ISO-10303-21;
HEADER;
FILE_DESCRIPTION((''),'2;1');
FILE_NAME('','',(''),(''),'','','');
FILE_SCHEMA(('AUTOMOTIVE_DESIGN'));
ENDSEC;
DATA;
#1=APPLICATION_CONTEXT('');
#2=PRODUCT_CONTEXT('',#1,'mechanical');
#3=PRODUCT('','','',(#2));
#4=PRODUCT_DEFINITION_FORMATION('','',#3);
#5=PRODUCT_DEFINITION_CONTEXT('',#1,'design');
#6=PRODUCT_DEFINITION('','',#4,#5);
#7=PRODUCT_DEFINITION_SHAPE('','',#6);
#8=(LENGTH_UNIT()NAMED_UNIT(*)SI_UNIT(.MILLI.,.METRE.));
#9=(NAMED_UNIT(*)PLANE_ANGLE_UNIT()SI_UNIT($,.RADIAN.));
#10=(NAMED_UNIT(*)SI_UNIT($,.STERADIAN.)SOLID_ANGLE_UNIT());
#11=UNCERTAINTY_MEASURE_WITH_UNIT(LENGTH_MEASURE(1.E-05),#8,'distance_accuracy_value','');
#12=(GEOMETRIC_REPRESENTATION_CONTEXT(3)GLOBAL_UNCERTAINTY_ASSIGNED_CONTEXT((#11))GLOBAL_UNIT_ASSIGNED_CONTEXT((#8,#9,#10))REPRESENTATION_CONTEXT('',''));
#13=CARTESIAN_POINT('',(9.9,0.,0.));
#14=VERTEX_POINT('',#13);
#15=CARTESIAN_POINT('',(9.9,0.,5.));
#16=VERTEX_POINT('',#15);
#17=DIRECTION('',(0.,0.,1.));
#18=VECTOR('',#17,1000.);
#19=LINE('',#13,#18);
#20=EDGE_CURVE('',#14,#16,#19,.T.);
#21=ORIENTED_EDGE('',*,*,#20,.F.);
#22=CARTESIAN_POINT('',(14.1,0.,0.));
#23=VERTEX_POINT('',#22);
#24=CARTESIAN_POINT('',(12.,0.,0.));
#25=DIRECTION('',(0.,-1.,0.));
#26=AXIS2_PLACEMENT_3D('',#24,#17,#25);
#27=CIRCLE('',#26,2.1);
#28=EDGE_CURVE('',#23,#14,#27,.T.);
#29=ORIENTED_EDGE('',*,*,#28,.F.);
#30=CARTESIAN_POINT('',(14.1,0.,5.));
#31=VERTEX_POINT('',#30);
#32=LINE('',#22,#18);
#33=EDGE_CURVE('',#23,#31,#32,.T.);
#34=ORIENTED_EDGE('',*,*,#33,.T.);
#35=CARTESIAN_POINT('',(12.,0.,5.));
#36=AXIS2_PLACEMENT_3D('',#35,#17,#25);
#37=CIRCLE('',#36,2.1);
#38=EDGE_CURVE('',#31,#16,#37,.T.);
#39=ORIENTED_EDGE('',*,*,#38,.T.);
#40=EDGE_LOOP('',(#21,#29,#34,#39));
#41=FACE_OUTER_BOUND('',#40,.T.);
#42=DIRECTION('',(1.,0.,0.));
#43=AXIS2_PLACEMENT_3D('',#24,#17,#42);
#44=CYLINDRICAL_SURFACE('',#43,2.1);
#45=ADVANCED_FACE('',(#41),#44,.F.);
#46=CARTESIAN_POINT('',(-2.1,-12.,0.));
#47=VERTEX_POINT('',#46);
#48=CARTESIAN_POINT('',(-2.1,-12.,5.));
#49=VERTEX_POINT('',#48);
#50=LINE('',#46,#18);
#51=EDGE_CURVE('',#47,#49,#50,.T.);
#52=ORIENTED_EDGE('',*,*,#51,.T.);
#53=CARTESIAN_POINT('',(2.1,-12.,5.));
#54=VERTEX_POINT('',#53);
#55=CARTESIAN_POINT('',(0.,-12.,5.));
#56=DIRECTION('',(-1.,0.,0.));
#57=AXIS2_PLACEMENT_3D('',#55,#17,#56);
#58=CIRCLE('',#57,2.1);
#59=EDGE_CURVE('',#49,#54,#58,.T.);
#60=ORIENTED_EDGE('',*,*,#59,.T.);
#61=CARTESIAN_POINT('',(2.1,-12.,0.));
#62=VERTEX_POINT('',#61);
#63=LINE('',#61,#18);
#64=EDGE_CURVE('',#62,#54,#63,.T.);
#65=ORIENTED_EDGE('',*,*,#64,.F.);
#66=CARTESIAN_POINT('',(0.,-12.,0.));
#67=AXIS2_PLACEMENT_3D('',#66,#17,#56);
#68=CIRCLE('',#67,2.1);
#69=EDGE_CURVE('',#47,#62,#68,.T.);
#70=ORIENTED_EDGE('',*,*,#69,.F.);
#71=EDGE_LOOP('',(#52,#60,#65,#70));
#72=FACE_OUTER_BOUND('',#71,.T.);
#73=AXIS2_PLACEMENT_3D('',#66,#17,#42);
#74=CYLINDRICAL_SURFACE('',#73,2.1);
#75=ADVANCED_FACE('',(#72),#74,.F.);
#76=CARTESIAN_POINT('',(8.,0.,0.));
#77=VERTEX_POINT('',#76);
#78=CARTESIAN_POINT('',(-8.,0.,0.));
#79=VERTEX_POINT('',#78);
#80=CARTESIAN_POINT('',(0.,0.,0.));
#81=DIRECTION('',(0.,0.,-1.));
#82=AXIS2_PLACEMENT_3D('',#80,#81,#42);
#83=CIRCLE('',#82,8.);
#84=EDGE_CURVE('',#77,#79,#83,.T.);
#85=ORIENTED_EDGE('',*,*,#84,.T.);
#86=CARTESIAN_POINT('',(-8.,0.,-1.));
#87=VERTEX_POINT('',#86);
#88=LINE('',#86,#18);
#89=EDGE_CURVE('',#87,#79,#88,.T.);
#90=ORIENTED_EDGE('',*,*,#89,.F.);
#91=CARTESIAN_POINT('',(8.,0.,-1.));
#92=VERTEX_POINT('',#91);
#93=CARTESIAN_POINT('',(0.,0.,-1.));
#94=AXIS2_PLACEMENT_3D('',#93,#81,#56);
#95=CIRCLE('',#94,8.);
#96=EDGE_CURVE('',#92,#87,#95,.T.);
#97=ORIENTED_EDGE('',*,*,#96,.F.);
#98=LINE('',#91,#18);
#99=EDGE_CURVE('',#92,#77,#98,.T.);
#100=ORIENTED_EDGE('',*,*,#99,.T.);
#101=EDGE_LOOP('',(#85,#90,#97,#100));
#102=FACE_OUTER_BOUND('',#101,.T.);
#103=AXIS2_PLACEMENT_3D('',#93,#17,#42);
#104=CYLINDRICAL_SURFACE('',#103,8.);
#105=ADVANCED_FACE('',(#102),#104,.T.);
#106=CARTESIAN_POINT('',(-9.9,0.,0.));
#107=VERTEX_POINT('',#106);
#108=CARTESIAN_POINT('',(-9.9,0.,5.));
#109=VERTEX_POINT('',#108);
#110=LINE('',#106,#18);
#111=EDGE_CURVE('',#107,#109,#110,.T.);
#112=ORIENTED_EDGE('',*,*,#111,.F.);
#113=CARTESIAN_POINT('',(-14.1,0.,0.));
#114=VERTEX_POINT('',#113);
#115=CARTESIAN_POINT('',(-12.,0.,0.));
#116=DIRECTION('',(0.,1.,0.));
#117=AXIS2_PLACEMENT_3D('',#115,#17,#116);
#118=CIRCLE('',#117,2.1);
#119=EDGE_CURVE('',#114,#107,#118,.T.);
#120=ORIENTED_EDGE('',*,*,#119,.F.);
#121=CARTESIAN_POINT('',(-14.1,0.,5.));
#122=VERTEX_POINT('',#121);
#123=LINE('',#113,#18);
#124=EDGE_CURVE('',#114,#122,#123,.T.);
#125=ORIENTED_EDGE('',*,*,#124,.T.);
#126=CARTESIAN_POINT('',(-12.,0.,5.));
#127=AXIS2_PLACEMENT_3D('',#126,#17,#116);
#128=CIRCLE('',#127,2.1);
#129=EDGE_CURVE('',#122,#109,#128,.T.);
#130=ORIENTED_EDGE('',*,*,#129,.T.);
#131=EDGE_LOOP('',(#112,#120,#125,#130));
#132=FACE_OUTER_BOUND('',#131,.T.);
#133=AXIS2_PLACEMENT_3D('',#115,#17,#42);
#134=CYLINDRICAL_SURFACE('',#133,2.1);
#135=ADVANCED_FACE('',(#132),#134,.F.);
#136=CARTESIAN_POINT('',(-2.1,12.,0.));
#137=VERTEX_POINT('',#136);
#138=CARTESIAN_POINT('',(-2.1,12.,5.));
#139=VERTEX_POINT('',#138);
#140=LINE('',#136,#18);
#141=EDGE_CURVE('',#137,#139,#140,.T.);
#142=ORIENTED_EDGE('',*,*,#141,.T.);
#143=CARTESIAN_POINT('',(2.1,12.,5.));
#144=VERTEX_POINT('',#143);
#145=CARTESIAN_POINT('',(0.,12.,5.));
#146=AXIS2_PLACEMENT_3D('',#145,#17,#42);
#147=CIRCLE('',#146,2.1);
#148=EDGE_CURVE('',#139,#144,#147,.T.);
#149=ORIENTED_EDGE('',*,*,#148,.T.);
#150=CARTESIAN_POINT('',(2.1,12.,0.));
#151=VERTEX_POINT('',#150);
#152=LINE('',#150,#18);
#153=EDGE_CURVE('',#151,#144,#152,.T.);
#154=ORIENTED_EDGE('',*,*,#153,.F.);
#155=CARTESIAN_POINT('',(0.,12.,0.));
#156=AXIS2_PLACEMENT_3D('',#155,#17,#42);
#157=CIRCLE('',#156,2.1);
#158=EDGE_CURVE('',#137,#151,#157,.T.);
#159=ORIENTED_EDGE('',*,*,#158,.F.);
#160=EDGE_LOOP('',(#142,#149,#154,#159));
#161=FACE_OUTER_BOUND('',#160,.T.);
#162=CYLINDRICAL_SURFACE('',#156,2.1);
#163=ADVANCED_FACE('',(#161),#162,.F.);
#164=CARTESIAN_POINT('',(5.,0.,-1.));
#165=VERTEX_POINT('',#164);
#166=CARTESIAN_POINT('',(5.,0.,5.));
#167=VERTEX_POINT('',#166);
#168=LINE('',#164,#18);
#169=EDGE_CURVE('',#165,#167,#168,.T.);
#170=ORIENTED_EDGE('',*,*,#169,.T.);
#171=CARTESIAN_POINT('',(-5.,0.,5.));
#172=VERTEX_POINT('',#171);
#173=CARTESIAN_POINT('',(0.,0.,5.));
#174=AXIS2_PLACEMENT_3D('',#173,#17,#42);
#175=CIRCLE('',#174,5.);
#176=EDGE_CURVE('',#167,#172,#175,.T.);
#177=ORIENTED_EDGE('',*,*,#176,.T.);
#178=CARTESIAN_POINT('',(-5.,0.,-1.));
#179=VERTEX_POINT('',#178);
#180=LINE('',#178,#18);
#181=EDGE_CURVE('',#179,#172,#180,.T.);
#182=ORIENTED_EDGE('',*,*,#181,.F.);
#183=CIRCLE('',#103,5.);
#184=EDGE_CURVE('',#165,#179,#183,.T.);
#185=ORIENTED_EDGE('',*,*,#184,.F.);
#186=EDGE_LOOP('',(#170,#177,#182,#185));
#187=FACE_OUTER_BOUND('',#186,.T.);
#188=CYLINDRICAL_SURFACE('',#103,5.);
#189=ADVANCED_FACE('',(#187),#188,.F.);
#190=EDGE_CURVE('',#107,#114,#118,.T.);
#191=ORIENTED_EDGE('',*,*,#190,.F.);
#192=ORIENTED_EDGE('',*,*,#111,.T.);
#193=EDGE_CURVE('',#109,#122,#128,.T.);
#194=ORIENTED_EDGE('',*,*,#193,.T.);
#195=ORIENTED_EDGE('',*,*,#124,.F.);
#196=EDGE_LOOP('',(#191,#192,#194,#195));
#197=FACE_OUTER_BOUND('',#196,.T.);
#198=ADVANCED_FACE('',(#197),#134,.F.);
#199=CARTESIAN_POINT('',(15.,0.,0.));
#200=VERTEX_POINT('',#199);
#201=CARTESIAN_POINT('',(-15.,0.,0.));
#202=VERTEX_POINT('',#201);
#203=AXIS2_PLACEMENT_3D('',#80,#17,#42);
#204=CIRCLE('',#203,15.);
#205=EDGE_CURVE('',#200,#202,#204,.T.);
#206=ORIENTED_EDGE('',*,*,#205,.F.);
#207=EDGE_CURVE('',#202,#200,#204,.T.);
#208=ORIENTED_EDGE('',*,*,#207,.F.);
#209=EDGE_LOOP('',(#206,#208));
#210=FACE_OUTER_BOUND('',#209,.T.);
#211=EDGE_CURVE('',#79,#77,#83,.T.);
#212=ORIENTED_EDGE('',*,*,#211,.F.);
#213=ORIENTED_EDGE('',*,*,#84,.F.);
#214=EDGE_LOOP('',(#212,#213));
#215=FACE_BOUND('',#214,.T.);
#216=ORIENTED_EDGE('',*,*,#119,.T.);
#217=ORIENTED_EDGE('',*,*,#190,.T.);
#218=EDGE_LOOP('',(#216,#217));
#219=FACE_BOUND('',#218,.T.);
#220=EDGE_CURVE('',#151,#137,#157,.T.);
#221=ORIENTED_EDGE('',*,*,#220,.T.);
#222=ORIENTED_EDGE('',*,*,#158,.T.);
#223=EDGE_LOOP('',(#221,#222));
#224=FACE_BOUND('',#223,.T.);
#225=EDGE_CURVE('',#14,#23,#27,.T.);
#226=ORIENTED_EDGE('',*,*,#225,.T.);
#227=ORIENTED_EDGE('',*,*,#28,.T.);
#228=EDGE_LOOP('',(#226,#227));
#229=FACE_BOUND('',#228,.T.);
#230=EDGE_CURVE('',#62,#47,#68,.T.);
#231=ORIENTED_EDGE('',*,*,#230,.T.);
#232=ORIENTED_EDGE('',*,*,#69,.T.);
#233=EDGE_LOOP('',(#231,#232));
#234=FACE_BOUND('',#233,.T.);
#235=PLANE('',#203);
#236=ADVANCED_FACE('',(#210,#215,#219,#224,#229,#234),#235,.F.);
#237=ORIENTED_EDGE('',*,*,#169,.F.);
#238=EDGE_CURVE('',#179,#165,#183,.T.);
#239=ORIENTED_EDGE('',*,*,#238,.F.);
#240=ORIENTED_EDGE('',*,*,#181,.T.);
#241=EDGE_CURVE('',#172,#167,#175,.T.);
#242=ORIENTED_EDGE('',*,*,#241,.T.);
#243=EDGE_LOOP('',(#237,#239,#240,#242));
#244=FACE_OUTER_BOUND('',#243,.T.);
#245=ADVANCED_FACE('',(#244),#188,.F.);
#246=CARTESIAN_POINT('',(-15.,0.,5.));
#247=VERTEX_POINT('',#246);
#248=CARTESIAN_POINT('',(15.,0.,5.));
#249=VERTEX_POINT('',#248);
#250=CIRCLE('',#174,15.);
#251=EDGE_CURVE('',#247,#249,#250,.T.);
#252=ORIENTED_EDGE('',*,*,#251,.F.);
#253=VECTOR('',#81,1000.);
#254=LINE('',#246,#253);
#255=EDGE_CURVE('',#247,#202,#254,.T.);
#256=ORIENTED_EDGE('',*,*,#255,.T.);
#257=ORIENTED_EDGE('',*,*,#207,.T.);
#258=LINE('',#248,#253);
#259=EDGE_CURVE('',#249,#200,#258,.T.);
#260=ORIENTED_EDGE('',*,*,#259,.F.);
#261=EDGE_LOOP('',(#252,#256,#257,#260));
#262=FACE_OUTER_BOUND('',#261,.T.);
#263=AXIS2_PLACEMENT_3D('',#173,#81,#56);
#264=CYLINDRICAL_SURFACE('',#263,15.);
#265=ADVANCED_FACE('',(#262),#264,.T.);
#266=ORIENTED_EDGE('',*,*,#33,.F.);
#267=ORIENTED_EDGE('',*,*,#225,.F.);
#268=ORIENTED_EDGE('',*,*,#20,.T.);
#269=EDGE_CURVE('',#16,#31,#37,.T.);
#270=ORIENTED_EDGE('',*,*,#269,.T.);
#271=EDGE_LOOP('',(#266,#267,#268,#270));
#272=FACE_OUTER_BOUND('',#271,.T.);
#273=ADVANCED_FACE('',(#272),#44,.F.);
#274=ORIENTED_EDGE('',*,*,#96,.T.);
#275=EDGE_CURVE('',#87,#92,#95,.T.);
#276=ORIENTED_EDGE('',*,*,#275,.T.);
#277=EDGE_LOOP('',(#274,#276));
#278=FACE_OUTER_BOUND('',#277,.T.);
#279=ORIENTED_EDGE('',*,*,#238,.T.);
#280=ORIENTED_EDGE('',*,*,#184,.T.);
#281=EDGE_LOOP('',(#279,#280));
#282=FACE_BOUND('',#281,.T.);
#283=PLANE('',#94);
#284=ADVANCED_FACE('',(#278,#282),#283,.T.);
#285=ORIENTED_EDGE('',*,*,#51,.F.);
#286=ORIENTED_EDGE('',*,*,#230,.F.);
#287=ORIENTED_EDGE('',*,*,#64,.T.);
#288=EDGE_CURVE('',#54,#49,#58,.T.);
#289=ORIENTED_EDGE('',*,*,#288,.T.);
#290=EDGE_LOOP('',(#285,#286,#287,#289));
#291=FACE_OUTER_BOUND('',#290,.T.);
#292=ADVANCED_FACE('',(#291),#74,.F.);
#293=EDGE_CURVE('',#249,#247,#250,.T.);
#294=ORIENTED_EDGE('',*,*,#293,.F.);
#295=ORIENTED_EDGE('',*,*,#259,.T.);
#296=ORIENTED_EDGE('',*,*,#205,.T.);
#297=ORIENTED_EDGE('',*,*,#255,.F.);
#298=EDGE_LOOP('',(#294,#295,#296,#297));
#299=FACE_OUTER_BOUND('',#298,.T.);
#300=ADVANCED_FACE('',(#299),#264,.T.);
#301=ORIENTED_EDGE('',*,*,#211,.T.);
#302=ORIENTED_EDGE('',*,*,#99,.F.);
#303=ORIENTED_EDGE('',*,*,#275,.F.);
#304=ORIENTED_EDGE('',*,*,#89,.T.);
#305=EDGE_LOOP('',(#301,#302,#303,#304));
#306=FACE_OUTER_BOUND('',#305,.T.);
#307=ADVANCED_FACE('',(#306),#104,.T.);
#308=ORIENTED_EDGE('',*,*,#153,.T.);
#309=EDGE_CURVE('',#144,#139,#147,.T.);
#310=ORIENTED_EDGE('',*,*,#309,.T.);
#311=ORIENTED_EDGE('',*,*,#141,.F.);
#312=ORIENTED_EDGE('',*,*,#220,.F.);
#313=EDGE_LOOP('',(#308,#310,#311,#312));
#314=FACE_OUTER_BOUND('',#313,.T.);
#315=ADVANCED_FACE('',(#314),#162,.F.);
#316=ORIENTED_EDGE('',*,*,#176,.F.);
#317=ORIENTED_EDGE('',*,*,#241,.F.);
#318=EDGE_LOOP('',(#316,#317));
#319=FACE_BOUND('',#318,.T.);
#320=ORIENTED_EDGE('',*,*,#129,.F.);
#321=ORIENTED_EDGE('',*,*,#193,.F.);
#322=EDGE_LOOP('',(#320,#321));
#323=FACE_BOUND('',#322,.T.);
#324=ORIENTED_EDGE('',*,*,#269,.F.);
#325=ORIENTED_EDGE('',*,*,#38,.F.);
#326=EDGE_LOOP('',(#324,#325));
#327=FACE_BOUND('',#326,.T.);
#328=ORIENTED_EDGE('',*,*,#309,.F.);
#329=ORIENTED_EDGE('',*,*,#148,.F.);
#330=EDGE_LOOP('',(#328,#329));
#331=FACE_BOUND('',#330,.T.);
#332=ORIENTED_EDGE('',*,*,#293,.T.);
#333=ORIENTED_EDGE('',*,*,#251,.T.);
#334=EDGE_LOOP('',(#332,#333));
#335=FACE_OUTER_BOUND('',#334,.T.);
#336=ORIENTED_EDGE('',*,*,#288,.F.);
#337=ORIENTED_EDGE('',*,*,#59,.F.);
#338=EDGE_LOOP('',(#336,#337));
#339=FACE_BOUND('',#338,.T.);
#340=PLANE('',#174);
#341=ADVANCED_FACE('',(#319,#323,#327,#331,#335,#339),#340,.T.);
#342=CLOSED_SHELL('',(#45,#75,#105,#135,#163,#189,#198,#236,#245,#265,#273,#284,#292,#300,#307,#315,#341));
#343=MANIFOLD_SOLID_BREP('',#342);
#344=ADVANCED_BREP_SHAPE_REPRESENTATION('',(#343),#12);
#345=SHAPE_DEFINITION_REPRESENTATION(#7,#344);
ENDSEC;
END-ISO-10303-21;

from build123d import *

# Parameters (mm, degrees)
SKETCH1_R           = 15
BOSS_EXTRUDE1_DEPTH = 5
SKETCH2_R           = 2.1
CUT_EXTRUDE1_DEPTH  = 22.794494718
CIRPATTERN1_COUNT   = 4
SKETCH3_R           = 8
BOSS_EXTRUDE2_DEPTH = 1
SKETCH4_R           = 5
CUT_EXTRUDE3_DEPTH  = 23.045407685


with BuildPart() as part:
    # Sketch1 → Boss-Extrude1 (new body)
    with BuildSketch(Plane.XY):
        Circle(SKETCH1_R)
    extrude(amount=BOSS_EXTRUDE1_DEPTH)

    # Sketch2 → Cut-Extrude1 (cut, through all)
    with BuildSketch(Plane.XY.offset(5)):
        with Locations((0, 12)):
            Circle(SKETCH2_R)
    cut_extrude1 = extrude(amount=-CUT_EXTRUDE1_DEPTH, mode=Mode.SUBTRACT)

    # CirPattern1: Cut-Extrude1 ×4 about axis
    cirpattern1_axis = Axis((0, 0, 0), (0, 0, 1))
    for i in range(1, CIRPATTERN1_COUNT):
        add(cut_extrude1.rotate(cirpattern1_axis, i * 360 / CIRPATTERN1_COUNT), mode=Mode.SUBTRACT)

    # Sketch3 → Boss-Extrude2 (add)
    with BuildSketch(Plane(origin=(0, 0, 0), x_dir=(-1, 0, 0), z_dir=(0, 0, -1))):
        with Locations(Location((0, 0, 0), (0, 0, 180))):
            Circle(SKETCH3_R)
    extrude(amount=BOSS_EXTRUDE2_DEPTH)

    # Sketch4 → Cut-Extrude3 (cut, through all)
    with BuildSketch(Plane.XY.offset(5)):
        Circle(SKETCH4_R)
    extrude(amount=-CUT_EXTRUDE3_DEPTH, mode=Mode.SUBTRACT)


solid = part.part
